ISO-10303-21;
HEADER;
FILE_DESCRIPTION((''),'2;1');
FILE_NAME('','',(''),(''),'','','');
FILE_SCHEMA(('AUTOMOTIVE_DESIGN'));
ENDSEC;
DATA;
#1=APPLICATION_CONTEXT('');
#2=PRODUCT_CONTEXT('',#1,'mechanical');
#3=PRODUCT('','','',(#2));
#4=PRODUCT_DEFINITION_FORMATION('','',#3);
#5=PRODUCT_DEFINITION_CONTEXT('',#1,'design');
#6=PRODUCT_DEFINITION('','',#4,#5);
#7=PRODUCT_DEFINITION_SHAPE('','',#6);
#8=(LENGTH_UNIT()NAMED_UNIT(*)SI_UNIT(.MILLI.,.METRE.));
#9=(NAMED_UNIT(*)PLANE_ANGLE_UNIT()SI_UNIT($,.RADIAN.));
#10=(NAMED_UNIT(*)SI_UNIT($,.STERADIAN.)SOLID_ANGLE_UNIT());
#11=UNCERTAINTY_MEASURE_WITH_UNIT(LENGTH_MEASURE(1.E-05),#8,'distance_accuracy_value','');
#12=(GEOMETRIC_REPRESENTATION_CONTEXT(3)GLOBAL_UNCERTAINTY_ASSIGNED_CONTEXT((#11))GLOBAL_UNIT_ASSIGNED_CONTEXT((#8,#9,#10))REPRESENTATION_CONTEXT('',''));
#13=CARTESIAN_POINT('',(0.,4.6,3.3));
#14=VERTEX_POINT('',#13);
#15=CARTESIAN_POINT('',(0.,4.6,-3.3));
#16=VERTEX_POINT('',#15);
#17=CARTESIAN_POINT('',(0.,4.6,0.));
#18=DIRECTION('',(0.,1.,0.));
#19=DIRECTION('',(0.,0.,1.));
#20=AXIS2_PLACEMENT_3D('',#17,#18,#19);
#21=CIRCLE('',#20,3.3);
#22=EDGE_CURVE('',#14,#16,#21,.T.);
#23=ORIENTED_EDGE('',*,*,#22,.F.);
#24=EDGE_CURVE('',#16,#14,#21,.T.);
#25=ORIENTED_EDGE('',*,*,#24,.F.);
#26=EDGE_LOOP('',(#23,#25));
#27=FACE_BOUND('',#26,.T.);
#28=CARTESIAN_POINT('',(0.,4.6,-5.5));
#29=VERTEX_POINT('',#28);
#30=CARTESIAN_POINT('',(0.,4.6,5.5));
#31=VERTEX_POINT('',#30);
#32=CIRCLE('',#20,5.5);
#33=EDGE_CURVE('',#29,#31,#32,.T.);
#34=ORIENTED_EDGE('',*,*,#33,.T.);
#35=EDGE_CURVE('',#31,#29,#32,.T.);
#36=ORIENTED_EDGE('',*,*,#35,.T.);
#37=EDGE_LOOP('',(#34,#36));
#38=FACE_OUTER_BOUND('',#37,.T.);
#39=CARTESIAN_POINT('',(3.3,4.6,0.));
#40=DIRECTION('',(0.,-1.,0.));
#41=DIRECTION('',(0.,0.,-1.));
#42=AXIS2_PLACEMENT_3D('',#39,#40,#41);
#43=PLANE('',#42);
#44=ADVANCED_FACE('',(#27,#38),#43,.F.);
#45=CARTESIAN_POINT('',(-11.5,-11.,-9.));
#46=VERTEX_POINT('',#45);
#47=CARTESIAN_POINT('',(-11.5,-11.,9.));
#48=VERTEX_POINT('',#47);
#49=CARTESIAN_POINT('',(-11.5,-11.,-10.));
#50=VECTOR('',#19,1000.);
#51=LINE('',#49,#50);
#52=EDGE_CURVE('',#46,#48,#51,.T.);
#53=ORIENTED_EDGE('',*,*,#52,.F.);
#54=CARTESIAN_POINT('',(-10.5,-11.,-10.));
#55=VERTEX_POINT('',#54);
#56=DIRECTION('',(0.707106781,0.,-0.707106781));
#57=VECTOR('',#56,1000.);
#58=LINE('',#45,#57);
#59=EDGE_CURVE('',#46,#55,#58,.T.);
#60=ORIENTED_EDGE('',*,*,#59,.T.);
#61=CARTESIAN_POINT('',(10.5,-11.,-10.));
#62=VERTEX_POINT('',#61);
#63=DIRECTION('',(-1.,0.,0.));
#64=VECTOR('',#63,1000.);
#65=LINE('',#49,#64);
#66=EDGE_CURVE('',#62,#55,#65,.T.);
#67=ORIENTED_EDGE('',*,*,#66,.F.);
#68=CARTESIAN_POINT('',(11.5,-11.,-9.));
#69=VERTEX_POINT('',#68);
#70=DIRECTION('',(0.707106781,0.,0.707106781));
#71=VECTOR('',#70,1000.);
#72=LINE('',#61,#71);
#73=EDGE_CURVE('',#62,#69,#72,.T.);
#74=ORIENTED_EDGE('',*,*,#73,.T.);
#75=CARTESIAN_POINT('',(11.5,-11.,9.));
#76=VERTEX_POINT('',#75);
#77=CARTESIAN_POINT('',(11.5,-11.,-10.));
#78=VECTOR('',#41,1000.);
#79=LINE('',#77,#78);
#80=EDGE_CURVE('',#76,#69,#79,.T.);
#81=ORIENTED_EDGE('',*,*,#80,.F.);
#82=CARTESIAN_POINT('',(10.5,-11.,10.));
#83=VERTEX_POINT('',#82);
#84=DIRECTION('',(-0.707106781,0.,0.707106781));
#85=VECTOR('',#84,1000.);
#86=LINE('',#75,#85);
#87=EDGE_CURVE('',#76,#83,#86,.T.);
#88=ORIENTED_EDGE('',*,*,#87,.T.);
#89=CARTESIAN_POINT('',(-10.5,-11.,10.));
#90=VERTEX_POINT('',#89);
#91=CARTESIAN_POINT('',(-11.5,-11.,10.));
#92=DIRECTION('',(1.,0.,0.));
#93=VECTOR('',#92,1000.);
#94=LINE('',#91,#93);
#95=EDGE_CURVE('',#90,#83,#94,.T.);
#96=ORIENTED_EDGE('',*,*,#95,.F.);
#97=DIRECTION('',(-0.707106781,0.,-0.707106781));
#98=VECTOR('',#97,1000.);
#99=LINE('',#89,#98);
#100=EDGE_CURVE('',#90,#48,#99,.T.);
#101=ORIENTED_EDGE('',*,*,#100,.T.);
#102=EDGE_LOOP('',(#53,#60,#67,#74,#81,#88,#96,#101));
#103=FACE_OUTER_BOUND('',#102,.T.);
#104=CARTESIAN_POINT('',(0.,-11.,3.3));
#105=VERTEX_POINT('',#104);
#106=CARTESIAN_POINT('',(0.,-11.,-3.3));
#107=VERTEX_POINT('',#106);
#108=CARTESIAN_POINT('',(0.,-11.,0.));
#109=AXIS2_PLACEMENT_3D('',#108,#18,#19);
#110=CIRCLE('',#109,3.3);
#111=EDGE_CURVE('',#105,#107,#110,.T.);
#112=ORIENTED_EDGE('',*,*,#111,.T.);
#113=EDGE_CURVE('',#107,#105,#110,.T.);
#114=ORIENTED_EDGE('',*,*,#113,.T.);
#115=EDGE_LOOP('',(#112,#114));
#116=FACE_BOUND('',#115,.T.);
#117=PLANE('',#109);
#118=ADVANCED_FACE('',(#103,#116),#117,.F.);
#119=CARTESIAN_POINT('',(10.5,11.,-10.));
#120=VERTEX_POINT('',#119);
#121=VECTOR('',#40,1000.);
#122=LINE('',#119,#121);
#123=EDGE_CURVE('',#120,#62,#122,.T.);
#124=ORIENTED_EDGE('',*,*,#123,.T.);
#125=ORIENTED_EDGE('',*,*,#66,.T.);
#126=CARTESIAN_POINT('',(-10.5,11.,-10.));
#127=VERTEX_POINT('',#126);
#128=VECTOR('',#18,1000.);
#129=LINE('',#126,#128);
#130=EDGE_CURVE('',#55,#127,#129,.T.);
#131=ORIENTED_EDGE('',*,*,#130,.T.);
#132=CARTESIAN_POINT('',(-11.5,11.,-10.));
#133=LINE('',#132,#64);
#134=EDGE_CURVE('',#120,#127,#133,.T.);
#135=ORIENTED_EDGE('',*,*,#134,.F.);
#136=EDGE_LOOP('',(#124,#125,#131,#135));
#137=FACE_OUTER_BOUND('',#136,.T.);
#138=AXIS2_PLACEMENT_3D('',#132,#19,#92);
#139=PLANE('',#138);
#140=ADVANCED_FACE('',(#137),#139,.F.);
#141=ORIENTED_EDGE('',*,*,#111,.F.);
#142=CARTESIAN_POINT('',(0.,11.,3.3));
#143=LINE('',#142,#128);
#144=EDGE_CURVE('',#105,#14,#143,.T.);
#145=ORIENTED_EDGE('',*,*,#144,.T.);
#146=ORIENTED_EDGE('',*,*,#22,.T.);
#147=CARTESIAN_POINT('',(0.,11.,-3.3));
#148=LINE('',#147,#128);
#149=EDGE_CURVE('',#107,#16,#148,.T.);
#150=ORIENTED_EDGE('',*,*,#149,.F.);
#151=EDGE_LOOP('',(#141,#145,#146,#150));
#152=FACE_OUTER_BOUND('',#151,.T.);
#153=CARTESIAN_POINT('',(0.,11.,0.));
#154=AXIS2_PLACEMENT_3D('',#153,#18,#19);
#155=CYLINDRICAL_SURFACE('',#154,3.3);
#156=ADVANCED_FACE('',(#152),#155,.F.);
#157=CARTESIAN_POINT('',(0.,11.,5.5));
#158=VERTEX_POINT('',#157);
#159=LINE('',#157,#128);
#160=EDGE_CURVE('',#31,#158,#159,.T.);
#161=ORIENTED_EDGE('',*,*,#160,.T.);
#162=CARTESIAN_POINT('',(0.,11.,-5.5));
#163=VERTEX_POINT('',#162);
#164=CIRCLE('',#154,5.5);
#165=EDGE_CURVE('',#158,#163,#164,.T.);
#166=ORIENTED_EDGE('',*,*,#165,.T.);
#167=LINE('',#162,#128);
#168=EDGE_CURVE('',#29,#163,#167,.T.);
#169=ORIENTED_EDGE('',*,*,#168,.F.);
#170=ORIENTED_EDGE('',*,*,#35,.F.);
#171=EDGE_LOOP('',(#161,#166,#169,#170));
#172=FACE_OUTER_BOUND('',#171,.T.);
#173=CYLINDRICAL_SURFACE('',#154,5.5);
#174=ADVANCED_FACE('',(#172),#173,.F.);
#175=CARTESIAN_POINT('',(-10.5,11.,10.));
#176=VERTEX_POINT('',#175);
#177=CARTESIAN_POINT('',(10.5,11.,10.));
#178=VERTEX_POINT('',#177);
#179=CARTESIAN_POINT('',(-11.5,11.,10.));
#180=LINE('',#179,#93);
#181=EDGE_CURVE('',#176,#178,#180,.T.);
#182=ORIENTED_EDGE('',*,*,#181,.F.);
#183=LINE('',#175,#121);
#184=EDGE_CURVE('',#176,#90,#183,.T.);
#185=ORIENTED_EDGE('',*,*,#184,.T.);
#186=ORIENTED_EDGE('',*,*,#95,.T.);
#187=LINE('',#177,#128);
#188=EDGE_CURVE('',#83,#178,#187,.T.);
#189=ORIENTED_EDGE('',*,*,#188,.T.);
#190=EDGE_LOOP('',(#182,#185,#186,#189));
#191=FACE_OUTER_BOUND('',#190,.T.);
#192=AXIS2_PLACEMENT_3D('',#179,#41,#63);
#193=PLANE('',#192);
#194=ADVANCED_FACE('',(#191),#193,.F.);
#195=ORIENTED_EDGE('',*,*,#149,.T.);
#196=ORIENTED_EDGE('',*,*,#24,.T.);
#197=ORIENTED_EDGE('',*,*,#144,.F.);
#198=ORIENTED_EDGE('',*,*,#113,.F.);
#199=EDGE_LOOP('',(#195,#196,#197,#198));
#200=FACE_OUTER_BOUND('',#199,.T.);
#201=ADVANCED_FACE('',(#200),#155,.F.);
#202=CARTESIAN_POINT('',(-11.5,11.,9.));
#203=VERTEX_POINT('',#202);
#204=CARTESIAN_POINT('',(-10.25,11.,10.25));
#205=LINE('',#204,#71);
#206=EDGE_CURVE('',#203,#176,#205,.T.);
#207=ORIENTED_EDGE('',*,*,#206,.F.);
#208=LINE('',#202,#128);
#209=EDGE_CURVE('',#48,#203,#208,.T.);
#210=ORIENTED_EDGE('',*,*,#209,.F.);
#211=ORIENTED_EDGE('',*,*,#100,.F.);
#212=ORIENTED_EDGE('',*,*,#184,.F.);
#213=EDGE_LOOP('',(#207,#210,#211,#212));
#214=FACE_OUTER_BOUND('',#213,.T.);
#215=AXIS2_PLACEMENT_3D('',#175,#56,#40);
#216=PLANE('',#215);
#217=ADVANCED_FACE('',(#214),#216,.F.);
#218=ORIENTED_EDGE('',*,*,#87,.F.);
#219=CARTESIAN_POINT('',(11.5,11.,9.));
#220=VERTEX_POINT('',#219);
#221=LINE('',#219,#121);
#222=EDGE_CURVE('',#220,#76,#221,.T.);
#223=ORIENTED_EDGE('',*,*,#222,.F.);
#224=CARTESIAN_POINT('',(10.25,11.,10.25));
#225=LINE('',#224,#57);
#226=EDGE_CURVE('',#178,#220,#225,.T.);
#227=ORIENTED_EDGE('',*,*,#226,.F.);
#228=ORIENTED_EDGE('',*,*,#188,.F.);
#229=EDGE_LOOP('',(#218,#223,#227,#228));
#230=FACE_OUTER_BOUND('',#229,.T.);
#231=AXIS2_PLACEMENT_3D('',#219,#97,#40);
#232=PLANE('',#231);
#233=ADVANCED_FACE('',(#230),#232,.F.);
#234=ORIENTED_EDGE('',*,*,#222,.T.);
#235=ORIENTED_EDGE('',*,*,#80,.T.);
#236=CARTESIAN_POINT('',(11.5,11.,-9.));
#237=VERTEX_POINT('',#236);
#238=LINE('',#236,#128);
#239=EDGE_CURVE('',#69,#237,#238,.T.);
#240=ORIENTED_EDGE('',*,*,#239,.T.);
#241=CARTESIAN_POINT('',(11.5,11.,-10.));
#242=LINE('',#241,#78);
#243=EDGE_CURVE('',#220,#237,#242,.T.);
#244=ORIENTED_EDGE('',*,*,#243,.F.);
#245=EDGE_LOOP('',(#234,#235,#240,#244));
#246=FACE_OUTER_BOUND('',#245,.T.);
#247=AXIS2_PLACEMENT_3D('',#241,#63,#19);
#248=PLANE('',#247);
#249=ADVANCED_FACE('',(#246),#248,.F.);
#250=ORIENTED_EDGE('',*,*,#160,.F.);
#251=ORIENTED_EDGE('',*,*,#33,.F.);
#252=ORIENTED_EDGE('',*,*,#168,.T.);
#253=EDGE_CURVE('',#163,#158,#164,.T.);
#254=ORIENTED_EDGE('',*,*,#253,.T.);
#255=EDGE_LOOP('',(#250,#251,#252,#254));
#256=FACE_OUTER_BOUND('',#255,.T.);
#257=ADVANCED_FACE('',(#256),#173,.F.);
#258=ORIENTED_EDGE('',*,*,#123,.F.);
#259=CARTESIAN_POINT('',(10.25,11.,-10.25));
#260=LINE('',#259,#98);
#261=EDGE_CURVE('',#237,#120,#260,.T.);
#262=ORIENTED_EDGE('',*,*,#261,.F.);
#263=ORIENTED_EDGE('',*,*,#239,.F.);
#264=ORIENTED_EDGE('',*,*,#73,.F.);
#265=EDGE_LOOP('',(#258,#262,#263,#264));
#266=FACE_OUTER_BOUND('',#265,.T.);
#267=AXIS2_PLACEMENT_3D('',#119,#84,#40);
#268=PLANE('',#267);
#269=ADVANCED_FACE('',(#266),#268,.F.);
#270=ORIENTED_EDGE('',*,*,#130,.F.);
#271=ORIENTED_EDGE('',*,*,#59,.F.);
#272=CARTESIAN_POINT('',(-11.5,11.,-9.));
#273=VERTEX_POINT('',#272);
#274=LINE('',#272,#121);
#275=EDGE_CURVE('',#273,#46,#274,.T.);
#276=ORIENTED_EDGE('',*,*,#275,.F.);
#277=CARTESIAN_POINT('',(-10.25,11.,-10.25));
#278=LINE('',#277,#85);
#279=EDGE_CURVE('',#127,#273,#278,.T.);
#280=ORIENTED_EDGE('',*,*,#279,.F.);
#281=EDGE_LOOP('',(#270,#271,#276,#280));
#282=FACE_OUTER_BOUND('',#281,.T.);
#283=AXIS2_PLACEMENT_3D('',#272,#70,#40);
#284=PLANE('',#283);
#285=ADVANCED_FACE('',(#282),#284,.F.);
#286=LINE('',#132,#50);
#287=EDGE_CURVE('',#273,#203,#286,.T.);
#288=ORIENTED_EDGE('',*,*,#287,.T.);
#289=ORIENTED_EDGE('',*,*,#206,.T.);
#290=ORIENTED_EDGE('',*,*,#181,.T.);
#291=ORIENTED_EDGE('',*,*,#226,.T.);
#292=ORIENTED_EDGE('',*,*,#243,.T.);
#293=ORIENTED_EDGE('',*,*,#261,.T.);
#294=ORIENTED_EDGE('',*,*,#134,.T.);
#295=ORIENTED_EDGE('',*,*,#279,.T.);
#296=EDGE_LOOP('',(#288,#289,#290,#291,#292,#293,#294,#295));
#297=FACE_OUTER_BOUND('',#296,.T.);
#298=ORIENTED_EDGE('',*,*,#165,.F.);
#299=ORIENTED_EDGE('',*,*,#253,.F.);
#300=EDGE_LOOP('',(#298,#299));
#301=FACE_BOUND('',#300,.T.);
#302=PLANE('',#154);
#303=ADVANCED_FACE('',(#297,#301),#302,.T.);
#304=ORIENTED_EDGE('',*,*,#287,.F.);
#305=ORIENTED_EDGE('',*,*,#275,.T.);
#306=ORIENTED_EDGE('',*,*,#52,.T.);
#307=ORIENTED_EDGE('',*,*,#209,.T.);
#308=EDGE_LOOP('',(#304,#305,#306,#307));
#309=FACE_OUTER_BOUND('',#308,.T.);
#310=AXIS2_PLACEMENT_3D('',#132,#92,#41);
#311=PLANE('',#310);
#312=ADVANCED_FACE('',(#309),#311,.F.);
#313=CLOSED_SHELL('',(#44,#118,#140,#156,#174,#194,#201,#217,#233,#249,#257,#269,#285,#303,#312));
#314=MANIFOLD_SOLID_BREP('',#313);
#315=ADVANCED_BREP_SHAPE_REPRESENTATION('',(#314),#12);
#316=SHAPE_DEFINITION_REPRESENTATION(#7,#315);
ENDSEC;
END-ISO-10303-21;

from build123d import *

# Parameters (mm, degrees)
SKETCH_1_W                   = 23
SKETCH_1_H                   = 20
EXTRUDE_1_DEPTH              = 11
HOLE_WIZARD_M6_1_D           = 6.6
HOLE_WIZARD_M6_1_CBORE_D     = 11
HOLE_WIZARD_M6_1_CBORE_DEPTH = 6.4
CHAMFER_1_SIZE               = 1


with BuildPart() as part:
    # 草图1 → 凸台-拉伸1 (new, symmetric)
    with BuildSketch(Plane(origin=(0, 0, 0), x_dir=(1, 0, 0), z_dir=(0, 1, 0))):
        Rectangle(SKETCH_1_W, SKETCH_1_H)
    extrude(amount=EXTRUDE_1_DEPTH, both=True)

    # M6 六角凹头螺钉的柱形沉头孔1 (through all)
    with Locations(Plane(origin=(0, 11, 0), x_dir=(1, 0, 0), z_dir=(0, 1, 0))):
        with Locations((0, 0)):
            CounterBoreHole(HOLE_WIZARD_M6_1_D / 2, HOLE_WIZARD_M6_1_CBORE_D / 2, HOLE_WIZARD_M6_1_CBORE_DEPTH)

    # 倒角1
    chamfer_1_edges = [part.edges().sort_by_distance(p)[0] for p in [
        (-11.5, 0, -10),
        (11.5, 0, -10),
        (11.5, 0, 10),
        (-11.5, 0, 10),
    ]]
    chamfer(chamfer_1_edges, length=CHAMFER_1_SIZE)


solid = part.part
